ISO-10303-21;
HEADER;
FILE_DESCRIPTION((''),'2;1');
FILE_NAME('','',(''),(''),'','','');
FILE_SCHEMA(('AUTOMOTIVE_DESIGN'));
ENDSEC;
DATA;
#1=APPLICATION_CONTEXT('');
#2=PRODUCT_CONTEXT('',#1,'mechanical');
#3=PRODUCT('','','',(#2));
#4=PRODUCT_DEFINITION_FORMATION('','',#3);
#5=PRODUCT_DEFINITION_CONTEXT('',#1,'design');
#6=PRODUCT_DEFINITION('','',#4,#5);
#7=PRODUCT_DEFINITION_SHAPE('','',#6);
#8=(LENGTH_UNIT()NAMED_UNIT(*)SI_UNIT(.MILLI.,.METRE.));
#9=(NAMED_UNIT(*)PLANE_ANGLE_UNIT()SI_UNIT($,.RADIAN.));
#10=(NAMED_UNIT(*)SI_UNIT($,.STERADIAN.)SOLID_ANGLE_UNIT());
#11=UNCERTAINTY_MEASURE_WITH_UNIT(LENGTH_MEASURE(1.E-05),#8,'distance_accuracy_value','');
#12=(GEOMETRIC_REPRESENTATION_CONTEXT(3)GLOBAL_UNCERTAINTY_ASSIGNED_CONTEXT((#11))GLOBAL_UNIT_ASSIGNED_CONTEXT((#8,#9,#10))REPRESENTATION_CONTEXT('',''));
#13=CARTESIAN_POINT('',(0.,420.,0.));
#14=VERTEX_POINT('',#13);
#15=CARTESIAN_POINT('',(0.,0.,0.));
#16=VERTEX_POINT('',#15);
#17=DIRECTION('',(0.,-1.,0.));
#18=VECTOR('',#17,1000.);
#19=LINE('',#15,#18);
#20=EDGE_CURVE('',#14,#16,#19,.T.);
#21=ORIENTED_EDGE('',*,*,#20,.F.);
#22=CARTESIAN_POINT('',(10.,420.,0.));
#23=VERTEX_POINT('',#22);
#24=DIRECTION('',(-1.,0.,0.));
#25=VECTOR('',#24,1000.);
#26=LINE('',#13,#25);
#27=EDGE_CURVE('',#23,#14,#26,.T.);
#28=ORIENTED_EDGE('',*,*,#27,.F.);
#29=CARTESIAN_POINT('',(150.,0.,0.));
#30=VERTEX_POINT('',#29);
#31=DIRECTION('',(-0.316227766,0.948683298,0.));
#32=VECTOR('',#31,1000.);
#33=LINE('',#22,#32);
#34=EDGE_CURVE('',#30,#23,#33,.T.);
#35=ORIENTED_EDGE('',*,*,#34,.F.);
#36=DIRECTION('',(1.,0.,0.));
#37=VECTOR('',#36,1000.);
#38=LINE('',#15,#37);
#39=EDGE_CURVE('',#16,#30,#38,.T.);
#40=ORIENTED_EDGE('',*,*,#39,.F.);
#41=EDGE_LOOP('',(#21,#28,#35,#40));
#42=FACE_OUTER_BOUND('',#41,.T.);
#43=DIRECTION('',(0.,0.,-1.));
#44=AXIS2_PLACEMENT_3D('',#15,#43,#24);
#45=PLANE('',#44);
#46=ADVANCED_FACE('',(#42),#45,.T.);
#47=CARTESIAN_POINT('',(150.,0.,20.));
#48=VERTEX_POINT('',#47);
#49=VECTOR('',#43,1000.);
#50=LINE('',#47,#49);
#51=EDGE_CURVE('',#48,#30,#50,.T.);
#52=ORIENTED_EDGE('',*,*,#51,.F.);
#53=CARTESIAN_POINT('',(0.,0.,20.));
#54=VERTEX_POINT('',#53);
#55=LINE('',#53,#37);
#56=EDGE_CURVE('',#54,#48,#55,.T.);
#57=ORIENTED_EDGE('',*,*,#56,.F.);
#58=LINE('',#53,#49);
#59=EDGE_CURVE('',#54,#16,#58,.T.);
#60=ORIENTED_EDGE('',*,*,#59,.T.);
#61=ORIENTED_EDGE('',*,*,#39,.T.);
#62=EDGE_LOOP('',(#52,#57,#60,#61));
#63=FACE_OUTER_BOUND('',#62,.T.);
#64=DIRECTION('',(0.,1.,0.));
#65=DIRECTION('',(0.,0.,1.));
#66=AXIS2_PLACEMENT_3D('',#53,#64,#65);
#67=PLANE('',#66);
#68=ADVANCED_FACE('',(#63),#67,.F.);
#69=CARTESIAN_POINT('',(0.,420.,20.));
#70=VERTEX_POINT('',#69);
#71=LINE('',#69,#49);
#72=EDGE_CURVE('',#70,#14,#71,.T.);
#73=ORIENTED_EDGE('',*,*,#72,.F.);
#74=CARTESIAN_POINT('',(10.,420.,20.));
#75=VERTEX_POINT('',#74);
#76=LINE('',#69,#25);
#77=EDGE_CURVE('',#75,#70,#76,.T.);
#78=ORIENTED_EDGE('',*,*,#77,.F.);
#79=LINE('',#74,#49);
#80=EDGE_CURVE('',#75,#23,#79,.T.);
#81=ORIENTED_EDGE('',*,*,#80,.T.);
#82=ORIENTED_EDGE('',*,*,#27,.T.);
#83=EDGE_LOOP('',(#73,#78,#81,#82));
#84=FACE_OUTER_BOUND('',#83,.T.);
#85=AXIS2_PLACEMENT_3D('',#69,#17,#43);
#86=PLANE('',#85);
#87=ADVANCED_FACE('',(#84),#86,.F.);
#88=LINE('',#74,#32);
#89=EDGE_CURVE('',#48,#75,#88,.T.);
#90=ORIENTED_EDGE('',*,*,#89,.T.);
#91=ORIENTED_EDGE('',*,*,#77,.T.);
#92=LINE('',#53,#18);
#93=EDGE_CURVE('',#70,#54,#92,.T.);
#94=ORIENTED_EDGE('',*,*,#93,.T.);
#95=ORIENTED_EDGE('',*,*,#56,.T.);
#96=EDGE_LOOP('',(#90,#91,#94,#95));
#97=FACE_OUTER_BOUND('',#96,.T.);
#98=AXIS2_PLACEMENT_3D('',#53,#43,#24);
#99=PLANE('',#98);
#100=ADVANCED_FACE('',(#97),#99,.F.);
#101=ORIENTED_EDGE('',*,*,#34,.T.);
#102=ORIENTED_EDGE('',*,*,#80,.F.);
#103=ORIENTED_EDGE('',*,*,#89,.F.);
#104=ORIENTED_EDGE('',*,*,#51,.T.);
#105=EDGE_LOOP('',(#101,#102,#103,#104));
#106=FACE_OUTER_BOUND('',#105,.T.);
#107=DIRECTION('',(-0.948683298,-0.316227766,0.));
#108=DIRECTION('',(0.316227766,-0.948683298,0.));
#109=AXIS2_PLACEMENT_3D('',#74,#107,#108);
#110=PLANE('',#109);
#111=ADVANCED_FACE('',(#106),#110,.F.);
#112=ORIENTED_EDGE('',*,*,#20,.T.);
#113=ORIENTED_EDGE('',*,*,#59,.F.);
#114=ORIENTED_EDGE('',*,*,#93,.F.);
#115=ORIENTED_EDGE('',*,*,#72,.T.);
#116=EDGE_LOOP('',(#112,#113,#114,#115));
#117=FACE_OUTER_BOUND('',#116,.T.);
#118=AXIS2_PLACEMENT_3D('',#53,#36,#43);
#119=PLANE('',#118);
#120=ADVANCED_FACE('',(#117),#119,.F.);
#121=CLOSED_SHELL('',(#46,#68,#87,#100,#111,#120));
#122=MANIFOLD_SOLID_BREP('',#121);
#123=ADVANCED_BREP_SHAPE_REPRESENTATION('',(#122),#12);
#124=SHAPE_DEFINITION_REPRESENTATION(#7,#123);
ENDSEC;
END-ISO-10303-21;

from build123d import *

# Parameters (mm, degrees)
BOSS_EXTRUDE1_DEPTH = 20


with BuildPart() as part:
    # Sketch1 → Boss-Extrude1 (new body)
    with BuildSketch(Plane.XY):
        Polygon((0, 0), (150, 0), (10, 420), (0, 420), align=None)
    extrude(amount=BOSS_EXTRUDE1_DEPTH)


solid = part.part
